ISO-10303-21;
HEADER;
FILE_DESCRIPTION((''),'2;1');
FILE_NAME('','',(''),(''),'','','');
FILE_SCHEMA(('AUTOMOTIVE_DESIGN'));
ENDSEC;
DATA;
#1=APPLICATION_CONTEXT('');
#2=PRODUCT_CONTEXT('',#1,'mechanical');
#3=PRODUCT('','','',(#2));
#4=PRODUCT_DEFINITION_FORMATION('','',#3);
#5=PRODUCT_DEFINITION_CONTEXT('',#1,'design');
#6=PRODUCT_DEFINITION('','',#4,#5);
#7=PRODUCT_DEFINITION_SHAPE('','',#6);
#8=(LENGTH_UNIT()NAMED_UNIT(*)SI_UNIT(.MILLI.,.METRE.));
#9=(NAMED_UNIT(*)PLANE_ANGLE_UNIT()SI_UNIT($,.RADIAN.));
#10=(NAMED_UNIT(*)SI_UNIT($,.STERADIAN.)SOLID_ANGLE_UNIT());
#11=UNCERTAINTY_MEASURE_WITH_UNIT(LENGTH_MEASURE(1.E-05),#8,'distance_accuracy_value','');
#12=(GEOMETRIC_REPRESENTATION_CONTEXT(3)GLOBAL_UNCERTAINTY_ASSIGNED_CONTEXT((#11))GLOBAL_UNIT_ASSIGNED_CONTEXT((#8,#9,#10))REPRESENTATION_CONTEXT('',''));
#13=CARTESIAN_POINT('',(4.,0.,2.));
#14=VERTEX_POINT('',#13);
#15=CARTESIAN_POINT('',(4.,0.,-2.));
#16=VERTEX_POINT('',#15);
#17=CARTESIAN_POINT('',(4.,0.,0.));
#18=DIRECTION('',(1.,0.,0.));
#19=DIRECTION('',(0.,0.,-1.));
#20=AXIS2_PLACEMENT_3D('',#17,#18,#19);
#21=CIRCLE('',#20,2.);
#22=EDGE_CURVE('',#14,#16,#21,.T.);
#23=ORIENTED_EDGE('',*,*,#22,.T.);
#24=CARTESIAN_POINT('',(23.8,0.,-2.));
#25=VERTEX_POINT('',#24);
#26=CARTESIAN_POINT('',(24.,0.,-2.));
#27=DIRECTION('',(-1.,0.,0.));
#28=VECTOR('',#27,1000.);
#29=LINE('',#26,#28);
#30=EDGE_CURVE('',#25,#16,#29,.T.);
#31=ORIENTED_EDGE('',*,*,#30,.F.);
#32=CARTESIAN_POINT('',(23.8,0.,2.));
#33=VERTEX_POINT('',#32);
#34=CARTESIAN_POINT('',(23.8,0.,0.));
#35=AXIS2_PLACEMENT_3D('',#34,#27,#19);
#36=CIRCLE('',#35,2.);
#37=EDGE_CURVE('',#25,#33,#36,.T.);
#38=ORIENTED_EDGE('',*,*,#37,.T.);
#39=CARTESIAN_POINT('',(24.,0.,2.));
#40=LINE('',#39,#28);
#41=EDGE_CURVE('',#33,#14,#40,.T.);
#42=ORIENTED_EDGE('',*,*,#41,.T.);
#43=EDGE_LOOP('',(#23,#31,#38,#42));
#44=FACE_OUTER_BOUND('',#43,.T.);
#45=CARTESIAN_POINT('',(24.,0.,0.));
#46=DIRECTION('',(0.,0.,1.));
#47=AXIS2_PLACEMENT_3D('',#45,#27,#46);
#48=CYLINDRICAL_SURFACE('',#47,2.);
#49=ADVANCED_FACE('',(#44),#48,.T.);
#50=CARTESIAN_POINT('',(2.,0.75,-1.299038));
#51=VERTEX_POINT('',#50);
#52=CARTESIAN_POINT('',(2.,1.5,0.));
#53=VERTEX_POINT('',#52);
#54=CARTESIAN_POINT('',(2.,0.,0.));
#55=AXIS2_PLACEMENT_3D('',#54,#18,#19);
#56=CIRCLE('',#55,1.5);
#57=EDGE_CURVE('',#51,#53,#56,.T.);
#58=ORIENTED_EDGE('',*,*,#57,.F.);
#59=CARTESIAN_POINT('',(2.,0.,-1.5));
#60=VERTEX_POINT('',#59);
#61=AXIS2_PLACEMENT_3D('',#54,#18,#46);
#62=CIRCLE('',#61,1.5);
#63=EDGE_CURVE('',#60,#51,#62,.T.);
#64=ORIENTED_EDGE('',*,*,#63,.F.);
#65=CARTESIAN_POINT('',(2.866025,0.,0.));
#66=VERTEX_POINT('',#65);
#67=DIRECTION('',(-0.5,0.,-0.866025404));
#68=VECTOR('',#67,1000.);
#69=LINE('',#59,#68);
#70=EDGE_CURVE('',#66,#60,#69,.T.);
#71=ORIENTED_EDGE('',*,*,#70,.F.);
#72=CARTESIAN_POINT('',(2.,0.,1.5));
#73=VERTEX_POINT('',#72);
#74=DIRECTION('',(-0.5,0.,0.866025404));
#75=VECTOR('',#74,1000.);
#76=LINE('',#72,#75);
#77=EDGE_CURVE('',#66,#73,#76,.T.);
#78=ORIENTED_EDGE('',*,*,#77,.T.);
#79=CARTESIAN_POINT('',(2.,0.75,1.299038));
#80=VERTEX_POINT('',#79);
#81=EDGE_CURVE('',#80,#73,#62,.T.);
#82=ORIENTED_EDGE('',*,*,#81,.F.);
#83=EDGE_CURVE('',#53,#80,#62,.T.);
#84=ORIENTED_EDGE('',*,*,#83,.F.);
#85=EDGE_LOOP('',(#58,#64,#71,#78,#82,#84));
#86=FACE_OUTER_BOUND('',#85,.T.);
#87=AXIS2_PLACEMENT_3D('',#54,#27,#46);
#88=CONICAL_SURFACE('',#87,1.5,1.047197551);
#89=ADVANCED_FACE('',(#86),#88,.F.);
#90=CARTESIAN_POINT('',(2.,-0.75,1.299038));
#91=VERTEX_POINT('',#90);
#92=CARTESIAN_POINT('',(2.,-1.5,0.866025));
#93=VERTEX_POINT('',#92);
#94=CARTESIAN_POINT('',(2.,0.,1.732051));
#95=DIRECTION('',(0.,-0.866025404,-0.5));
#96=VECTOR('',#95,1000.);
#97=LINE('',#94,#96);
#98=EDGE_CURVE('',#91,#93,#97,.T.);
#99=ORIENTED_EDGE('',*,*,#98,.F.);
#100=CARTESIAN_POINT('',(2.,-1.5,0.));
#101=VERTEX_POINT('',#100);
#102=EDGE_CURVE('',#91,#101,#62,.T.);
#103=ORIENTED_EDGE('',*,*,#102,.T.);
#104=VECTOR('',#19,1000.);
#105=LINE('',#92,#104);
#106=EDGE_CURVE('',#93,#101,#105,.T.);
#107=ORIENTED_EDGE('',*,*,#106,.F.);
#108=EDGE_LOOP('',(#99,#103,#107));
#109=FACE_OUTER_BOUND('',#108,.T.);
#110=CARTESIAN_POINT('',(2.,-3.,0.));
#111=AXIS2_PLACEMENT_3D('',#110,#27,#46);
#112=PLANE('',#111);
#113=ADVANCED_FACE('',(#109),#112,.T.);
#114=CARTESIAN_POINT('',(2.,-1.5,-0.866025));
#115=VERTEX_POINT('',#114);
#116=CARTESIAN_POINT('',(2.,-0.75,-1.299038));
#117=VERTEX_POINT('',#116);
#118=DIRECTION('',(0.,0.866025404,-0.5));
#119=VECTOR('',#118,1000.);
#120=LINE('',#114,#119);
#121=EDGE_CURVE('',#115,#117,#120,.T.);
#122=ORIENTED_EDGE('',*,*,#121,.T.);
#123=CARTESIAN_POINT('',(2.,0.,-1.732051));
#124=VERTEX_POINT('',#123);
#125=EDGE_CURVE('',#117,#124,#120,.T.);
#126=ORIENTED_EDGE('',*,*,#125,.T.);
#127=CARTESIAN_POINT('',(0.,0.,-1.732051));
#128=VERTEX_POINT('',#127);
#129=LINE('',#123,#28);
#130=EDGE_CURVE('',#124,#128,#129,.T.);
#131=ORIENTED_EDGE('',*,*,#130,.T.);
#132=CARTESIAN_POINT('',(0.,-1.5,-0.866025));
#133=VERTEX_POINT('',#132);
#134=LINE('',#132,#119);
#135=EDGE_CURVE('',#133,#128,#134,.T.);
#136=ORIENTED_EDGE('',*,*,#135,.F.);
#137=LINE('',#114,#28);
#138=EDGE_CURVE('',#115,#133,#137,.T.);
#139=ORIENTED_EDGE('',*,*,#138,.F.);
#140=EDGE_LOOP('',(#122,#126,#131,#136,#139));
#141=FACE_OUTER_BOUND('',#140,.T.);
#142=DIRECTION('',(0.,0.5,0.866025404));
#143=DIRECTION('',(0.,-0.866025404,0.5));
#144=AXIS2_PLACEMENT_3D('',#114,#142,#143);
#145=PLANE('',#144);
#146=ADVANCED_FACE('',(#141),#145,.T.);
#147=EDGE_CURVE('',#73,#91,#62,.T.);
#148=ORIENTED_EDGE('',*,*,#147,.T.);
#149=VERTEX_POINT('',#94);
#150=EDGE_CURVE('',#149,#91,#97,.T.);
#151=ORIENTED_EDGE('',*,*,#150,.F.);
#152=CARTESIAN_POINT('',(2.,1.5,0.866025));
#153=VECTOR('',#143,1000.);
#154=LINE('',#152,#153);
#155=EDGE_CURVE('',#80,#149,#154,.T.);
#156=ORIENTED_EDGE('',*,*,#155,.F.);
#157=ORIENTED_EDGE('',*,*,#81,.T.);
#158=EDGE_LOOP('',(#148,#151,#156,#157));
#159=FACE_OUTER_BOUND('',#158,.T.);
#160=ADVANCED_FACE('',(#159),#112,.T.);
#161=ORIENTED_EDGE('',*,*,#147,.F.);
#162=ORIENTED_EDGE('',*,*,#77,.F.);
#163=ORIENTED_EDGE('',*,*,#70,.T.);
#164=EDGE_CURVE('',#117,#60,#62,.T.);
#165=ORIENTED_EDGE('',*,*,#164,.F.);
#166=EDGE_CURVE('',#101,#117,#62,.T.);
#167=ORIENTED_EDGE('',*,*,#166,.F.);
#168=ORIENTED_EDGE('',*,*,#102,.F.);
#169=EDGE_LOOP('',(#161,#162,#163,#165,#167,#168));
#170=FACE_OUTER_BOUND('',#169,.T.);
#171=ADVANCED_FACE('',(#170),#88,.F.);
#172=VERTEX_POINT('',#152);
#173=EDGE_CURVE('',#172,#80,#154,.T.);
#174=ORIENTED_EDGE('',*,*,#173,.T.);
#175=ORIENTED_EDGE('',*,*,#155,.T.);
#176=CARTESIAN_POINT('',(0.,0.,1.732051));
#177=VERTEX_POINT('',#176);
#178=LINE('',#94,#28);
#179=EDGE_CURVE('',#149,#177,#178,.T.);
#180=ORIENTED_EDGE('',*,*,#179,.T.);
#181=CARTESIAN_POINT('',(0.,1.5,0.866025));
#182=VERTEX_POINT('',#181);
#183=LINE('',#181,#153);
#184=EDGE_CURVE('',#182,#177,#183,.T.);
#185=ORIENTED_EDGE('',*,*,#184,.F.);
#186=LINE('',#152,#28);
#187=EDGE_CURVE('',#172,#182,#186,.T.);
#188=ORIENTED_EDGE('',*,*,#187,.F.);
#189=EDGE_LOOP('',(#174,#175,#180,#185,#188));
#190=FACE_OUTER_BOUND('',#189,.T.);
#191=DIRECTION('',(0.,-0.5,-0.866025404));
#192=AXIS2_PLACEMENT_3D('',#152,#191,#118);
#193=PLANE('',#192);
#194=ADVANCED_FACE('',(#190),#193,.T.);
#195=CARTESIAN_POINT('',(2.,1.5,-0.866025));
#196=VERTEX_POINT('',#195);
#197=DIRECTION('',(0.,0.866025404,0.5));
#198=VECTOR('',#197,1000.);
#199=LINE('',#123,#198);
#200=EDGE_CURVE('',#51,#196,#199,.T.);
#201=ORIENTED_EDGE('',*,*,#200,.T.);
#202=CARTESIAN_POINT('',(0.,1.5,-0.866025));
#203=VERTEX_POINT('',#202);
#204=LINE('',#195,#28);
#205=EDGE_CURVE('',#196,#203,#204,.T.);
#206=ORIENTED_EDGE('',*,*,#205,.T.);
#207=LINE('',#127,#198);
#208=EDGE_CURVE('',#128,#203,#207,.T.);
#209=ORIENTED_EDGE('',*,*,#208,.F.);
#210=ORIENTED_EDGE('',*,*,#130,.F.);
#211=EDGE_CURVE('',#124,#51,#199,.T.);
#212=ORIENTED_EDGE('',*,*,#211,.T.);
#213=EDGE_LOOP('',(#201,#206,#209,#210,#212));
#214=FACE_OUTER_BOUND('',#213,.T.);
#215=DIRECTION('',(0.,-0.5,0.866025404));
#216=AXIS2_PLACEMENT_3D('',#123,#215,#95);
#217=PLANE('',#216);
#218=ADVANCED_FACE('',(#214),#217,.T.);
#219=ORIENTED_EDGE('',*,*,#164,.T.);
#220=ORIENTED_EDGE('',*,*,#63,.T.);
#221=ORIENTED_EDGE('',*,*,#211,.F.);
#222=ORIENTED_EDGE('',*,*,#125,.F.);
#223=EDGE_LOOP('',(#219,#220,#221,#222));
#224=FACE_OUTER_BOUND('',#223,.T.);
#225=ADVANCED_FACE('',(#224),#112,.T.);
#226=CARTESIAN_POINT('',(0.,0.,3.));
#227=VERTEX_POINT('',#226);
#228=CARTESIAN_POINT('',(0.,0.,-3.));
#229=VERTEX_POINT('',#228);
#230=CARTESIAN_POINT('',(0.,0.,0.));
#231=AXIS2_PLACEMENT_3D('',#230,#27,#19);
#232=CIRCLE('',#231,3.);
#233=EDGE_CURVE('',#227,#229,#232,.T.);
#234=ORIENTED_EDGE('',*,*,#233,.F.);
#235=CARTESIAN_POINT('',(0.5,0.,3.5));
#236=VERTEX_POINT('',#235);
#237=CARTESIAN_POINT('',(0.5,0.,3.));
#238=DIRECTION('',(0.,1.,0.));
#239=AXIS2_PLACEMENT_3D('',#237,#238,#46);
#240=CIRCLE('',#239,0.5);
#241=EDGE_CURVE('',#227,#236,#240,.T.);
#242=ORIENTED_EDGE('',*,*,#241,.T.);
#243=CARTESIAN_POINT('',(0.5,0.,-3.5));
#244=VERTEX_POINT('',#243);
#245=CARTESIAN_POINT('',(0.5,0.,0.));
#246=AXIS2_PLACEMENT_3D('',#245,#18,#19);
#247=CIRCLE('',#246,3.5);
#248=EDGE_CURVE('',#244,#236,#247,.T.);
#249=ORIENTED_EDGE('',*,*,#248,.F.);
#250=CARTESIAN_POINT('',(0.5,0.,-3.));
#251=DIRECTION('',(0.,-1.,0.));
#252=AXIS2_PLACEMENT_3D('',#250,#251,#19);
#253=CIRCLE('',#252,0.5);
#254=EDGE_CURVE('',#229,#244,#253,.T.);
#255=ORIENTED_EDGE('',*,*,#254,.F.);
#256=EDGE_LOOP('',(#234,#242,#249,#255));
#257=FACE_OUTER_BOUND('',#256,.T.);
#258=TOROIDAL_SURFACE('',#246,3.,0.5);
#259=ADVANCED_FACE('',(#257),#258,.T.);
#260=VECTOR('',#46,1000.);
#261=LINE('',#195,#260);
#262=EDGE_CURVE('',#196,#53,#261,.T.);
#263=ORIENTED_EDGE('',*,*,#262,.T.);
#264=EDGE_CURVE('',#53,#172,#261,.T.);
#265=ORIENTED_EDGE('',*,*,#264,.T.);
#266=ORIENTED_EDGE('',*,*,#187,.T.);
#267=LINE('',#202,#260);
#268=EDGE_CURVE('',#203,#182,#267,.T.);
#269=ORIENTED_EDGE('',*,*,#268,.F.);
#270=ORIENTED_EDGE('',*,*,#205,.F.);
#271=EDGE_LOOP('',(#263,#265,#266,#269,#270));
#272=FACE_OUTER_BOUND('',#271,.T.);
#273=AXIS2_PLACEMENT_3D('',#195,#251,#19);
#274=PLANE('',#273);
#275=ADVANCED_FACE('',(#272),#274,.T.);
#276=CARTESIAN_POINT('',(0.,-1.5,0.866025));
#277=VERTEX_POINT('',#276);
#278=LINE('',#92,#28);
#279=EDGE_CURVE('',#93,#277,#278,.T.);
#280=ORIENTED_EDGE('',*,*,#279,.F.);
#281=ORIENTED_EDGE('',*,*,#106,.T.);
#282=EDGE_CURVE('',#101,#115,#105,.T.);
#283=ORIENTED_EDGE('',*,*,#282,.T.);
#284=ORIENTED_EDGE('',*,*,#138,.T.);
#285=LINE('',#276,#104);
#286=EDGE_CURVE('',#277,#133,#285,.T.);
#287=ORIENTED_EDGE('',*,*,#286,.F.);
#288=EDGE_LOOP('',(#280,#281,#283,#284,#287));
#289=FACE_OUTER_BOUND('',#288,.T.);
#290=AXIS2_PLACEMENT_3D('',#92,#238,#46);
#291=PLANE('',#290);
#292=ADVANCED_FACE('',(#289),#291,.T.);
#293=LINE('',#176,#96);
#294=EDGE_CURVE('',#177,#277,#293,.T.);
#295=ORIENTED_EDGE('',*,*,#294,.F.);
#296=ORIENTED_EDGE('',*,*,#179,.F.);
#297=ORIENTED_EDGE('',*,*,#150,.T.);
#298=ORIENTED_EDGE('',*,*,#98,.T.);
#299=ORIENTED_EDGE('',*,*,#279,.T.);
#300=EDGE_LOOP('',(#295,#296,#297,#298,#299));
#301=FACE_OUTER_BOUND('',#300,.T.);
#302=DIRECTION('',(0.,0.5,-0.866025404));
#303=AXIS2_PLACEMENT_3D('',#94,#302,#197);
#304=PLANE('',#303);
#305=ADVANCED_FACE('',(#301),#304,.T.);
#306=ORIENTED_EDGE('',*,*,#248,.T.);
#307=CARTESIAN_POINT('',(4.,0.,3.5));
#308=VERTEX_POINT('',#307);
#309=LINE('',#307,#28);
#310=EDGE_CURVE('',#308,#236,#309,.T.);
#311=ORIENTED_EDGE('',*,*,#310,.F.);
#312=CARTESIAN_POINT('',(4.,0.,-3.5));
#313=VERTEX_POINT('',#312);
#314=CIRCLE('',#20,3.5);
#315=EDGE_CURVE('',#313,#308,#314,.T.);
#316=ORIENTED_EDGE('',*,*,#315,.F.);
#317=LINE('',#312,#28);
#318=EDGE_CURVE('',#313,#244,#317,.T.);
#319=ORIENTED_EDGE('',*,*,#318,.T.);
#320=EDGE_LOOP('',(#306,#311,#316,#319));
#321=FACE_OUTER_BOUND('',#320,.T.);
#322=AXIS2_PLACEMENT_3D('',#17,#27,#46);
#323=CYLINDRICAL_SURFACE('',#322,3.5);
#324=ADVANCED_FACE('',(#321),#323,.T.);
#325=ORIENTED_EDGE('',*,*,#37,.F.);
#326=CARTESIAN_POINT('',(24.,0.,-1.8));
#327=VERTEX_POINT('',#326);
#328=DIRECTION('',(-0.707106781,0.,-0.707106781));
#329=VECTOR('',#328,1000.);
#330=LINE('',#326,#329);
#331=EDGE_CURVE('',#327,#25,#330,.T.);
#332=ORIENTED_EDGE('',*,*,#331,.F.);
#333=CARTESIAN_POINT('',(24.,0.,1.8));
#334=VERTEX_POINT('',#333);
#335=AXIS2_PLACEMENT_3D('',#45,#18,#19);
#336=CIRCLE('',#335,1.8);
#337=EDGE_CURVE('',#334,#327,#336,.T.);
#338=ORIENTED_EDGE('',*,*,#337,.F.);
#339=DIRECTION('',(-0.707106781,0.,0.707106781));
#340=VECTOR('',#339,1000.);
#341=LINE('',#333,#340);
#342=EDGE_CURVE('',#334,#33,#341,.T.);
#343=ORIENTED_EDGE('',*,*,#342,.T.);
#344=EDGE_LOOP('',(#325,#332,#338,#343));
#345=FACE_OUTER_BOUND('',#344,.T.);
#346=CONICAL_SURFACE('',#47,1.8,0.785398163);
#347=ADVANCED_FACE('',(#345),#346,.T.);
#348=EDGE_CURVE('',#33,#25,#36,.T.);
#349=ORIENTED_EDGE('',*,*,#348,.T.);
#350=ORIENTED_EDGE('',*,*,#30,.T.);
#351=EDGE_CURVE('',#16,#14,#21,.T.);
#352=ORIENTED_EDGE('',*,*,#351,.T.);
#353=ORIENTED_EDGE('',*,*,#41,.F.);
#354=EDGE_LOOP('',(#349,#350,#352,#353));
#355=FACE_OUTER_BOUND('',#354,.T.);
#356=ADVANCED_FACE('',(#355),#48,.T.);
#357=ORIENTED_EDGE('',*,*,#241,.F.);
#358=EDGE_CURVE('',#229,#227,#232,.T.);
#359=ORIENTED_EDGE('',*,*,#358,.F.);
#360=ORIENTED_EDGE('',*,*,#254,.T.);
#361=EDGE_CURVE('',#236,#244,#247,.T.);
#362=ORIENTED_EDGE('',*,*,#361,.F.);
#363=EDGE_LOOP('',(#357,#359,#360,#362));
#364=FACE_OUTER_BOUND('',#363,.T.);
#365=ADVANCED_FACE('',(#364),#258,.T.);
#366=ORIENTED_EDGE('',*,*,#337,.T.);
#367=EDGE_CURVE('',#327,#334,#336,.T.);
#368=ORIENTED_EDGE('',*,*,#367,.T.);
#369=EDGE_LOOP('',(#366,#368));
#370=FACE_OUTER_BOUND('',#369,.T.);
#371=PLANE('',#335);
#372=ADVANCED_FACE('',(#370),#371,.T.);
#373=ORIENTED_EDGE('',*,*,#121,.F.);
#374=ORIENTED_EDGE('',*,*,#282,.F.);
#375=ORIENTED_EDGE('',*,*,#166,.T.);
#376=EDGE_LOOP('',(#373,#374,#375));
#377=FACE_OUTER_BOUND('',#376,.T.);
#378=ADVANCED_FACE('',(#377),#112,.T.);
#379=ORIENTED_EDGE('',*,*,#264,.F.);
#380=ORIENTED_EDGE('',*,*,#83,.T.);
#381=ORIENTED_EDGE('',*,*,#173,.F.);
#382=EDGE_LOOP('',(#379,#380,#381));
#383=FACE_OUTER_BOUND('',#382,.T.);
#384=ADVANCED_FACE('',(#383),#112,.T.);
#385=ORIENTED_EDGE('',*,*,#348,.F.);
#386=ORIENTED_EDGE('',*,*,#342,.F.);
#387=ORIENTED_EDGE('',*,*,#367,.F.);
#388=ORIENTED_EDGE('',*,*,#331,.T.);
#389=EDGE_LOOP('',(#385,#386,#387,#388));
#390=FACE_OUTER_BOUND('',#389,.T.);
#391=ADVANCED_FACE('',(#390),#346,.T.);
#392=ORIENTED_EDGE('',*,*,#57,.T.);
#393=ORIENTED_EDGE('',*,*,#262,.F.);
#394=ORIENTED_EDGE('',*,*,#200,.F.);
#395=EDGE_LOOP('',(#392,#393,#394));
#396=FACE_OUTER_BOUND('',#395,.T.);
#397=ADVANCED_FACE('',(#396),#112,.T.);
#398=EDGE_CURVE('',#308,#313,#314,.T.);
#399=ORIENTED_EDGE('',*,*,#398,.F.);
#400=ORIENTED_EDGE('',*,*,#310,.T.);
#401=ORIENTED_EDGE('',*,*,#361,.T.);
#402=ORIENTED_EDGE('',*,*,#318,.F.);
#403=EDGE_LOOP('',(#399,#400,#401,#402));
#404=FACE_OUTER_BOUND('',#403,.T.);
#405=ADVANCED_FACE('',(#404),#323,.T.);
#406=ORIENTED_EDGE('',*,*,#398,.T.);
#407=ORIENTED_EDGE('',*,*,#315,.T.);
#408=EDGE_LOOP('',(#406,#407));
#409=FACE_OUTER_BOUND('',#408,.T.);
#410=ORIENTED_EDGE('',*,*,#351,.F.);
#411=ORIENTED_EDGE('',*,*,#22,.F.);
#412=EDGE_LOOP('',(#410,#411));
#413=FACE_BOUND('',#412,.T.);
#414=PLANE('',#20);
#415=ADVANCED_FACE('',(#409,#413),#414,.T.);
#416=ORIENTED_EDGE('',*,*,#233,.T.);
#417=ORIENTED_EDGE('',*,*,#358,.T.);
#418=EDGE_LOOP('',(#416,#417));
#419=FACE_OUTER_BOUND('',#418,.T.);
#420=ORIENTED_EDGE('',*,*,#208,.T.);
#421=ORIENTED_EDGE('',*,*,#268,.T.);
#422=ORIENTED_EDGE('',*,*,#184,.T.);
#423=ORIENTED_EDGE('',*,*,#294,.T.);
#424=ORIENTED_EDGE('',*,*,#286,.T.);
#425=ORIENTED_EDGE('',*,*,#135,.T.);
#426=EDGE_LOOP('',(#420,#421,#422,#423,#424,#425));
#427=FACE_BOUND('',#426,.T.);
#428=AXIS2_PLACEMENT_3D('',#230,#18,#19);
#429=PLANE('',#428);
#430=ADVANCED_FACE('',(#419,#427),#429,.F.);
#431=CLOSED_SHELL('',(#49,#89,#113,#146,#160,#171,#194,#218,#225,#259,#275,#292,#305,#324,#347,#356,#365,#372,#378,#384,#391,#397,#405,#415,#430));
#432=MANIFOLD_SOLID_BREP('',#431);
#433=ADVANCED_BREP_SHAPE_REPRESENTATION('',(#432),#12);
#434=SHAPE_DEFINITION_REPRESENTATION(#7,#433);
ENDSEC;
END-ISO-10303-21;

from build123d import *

# Parameters (mm, degrees)
SKETCH1_R           = 3.5
BASEHEAD_DEPTH      = 4
SKETCH2_R           = 2
BASEBODY_DEPTH      = 20
HEXAGONSOCKET_DEPTH = 2
TOPFILLET_R         = 0.5
CHAMFER1_SIZE       = 0.2


with BuildPart() as part:
    # Sketch1 → BaseHead (new body)
    with BuildSketch(Plane(origin=(0, 0, 0), x_dir=(0, 0, -1), z_dir=(1, 0, 0))):
        Circle(SKETCH1_R)
    extrude(amount=BASEHEAD_DEPTH)

    # Sketch2 → BaseBody (add)
    with BuildSketch(Plane(origin=(4, 0, 0), x_dir=(0, 0, -1), z_dir=(1, 0, 0))):
        Circle(SKETCH2_R)
    extrude(amount=BASEBODY_DEPTH)

    # Sketch3 → HexagonSocket (cut)
    with BuildSketch(Plane(origin=(0, 0, 0), x_dir=(0, 0, -1), z_dir=(1, 0, 0))):
        Polygon((1.732050808, 0), (0.866025404, 1.5), (-0.866025404, 1.5), (-1.732050808, 0), (-0.866025404, -1.5), (0.866025404, -1.5), align=None)
    extrude(amount=HEXAGONSOCKET_DEPTH, mode=Mode.SUBTRACT)

    # Sketch4 → Cut-Revolve1 (revolve, cut)
    with BuildSketch(Plane(origin=(-4.19613823, 0.75, 0), x_dir=(-1, 0, 0), z_dir=(0, 0, 1)), mode=Mode.PRIVATE) as cut_revolve1_sk:
        Polygon((-6.19613823, 2.25), (-7.062163633, 0.75), (-6.19613823, 0.75), align=None)
    revolve(cut_revolve1_sk.sketch.rotate(Axis((0.838992387, 0, 0), (-1, 0, 0)), 90), axis=Axis((0.838992387, 0, 0), (-1, 0, 0)), mode=Mode.SUBTRACT)

    # TopFillet
    topfillet_edges = [part.edges().sort_by_distance(p)[0] for p in [
        (0, 0, 3.5),
    ]]
    fillet(topfillet_edges, radius=TOPFILLET_R)

    # Chamfer1
    chamfer1_edges = [part.edges().sort_by_distance(p)[0] for p in [
        (24, 0, 2),
    ]]
    chamfer(chamfer1_edges, length=CHAMFER1_SIZE)


solid = part.part
